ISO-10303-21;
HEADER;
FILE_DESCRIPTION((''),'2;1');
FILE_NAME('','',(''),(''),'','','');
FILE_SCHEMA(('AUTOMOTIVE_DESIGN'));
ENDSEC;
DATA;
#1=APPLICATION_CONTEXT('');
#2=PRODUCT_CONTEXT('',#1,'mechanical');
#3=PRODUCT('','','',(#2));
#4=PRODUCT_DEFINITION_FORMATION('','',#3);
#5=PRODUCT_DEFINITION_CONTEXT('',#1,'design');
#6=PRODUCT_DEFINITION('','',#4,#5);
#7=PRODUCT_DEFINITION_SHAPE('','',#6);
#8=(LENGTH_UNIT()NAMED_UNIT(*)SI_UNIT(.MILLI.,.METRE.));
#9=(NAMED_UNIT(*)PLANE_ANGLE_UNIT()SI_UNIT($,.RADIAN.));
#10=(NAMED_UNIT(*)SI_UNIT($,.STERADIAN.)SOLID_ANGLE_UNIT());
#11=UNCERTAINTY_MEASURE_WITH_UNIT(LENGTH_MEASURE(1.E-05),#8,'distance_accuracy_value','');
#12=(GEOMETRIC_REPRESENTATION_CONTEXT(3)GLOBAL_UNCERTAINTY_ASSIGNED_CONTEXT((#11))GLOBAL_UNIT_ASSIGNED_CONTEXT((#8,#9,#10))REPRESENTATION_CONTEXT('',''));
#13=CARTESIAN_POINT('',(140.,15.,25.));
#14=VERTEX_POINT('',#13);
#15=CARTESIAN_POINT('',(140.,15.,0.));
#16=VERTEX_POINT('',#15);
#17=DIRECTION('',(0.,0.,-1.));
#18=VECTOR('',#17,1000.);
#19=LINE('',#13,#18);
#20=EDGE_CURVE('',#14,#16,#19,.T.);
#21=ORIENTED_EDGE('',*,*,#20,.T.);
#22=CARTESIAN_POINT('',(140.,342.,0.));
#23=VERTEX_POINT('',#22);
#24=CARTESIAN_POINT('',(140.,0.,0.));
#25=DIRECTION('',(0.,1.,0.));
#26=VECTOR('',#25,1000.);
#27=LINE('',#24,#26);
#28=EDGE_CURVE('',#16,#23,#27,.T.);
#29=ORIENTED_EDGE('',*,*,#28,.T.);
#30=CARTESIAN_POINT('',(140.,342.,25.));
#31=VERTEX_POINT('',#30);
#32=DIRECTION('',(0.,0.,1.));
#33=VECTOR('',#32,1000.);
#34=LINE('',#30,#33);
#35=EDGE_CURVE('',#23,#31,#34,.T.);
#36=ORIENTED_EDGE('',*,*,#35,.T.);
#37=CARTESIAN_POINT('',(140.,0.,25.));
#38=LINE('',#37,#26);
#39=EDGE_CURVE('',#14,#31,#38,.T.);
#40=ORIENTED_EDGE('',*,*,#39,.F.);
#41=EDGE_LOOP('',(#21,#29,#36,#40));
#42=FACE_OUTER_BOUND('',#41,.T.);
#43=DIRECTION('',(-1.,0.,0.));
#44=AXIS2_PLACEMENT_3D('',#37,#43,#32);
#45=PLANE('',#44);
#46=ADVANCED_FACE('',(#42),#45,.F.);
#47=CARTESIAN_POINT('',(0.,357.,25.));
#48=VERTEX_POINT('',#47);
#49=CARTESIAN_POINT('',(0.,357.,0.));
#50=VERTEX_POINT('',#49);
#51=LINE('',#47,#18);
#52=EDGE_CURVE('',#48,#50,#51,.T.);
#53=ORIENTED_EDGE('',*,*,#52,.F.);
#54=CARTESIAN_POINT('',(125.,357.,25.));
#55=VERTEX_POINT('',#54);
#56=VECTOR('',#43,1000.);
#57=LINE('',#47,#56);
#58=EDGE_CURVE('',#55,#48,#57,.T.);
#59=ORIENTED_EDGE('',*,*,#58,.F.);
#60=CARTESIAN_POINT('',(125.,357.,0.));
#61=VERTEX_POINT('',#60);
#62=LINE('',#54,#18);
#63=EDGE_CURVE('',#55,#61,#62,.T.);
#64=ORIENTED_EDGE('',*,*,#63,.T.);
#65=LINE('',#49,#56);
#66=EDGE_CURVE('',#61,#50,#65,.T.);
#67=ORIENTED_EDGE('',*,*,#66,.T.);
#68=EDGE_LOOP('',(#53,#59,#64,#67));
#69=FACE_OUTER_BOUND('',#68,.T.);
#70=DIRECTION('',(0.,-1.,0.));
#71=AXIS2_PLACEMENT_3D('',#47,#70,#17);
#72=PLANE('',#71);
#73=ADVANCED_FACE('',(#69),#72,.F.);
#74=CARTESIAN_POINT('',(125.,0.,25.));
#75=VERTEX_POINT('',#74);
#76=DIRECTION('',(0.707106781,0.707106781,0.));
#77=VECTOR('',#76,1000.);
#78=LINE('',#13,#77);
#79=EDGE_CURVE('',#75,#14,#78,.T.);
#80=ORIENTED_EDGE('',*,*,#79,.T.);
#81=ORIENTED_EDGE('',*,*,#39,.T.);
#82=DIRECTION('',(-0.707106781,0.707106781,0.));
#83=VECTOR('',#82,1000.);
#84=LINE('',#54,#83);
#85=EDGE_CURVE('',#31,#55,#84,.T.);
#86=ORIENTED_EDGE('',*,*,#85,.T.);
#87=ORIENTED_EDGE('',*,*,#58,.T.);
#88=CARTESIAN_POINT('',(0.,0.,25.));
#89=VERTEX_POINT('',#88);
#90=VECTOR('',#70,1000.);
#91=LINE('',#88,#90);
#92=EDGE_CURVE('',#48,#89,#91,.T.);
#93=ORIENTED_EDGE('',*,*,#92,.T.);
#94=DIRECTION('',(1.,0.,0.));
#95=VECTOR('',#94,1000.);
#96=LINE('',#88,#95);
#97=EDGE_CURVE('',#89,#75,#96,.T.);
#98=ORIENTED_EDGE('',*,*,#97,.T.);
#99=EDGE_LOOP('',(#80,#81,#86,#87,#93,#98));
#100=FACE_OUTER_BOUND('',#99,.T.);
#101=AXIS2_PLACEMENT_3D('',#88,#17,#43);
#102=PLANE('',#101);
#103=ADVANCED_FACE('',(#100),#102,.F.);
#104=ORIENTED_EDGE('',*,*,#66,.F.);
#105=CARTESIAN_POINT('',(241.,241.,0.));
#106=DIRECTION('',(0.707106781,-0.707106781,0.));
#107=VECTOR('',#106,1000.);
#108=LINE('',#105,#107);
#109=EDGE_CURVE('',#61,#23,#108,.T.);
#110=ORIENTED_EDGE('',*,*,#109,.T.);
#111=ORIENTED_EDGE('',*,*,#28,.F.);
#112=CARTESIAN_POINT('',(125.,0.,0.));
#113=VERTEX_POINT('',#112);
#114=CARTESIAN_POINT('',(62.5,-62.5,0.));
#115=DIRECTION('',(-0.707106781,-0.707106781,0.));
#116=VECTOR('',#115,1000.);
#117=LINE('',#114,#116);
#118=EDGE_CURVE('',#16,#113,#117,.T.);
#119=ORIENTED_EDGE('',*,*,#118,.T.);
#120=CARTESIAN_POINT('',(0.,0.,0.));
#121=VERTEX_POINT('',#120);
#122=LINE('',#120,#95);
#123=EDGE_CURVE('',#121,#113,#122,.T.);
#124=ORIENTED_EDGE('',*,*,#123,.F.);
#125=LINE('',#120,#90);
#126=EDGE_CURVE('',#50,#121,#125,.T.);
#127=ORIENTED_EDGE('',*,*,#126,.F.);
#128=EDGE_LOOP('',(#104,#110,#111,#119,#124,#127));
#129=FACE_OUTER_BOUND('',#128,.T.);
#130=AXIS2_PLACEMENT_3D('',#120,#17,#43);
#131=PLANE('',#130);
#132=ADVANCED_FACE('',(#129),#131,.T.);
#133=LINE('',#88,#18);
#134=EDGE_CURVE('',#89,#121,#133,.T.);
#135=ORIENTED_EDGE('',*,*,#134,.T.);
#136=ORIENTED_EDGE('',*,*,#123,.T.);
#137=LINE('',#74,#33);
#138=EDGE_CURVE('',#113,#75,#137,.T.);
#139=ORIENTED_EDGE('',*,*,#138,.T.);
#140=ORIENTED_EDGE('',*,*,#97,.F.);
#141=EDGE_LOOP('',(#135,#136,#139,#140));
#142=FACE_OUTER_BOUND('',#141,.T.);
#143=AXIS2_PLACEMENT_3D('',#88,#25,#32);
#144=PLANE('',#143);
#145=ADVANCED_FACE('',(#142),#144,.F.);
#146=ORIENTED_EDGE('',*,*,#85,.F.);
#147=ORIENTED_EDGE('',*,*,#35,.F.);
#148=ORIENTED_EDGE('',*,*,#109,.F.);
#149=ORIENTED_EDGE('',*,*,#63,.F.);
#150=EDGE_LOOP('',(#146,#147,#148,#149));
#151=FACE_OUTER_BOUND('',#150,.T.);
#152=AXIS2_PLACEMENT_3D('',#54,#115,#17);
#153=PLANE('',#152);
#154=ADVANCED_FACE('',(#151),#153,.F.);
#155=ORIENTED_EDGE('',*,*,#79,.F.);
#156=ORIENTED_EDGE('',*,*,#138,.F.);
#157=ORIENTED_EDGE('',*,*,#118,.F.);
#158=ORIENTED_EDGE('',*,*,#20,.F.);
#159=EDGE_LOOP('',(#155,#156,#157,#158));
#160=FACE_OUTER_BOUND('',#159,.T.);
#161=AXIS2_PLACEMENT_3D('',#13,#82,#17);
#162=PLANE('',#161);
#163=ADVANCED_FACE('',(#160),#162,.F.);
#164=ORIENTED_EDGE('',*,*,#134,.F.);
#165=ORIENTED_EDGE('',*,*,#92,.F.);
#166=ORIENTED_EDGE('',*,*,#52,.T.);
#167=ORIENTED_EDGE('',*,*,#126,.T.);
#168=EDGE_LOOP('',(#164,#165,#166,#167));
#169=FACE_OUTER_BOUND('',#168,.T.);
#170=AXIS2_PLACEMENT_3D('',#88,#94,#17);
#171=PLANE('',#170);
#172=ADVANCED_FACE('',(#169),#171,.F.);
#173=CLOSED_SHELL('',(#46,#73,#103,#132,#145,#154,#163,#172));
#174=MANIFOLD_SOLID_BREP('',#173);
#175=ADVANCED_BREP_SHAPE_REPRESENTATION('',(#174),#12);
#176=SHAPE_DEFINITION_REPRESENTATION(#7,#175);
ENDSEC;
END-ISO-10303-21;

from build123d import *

# Parameters (mm, degrees)
SKETCH1_W           = 140
SKETCH1_H           = 357
BOSS_EXTRUDE1_DEPTH = 25
CHAMFER2_SIZE       = 15


with BuildPart() as part:
    # Sketch1 → Boss-Extrude1 (new body)
    with BuildSketch(Plane.XY):
        with Locations((70, 178.5)):
            Rectangle(SKETCH1_W, SKETCH1_H)
    extrude(amount=BOSS_EXTRUDE1_DEPTH)

    # Chamfer2
    chamfer2_edges = [part.edges().sort_by_distance(p)[0] for p in [
        (140, 357, 12.5),
        (140, 0, 12.5),
    ]]
    chamfer(chamfer2_edges, length=CHAMFER2_SIZE)


solid = part.part
